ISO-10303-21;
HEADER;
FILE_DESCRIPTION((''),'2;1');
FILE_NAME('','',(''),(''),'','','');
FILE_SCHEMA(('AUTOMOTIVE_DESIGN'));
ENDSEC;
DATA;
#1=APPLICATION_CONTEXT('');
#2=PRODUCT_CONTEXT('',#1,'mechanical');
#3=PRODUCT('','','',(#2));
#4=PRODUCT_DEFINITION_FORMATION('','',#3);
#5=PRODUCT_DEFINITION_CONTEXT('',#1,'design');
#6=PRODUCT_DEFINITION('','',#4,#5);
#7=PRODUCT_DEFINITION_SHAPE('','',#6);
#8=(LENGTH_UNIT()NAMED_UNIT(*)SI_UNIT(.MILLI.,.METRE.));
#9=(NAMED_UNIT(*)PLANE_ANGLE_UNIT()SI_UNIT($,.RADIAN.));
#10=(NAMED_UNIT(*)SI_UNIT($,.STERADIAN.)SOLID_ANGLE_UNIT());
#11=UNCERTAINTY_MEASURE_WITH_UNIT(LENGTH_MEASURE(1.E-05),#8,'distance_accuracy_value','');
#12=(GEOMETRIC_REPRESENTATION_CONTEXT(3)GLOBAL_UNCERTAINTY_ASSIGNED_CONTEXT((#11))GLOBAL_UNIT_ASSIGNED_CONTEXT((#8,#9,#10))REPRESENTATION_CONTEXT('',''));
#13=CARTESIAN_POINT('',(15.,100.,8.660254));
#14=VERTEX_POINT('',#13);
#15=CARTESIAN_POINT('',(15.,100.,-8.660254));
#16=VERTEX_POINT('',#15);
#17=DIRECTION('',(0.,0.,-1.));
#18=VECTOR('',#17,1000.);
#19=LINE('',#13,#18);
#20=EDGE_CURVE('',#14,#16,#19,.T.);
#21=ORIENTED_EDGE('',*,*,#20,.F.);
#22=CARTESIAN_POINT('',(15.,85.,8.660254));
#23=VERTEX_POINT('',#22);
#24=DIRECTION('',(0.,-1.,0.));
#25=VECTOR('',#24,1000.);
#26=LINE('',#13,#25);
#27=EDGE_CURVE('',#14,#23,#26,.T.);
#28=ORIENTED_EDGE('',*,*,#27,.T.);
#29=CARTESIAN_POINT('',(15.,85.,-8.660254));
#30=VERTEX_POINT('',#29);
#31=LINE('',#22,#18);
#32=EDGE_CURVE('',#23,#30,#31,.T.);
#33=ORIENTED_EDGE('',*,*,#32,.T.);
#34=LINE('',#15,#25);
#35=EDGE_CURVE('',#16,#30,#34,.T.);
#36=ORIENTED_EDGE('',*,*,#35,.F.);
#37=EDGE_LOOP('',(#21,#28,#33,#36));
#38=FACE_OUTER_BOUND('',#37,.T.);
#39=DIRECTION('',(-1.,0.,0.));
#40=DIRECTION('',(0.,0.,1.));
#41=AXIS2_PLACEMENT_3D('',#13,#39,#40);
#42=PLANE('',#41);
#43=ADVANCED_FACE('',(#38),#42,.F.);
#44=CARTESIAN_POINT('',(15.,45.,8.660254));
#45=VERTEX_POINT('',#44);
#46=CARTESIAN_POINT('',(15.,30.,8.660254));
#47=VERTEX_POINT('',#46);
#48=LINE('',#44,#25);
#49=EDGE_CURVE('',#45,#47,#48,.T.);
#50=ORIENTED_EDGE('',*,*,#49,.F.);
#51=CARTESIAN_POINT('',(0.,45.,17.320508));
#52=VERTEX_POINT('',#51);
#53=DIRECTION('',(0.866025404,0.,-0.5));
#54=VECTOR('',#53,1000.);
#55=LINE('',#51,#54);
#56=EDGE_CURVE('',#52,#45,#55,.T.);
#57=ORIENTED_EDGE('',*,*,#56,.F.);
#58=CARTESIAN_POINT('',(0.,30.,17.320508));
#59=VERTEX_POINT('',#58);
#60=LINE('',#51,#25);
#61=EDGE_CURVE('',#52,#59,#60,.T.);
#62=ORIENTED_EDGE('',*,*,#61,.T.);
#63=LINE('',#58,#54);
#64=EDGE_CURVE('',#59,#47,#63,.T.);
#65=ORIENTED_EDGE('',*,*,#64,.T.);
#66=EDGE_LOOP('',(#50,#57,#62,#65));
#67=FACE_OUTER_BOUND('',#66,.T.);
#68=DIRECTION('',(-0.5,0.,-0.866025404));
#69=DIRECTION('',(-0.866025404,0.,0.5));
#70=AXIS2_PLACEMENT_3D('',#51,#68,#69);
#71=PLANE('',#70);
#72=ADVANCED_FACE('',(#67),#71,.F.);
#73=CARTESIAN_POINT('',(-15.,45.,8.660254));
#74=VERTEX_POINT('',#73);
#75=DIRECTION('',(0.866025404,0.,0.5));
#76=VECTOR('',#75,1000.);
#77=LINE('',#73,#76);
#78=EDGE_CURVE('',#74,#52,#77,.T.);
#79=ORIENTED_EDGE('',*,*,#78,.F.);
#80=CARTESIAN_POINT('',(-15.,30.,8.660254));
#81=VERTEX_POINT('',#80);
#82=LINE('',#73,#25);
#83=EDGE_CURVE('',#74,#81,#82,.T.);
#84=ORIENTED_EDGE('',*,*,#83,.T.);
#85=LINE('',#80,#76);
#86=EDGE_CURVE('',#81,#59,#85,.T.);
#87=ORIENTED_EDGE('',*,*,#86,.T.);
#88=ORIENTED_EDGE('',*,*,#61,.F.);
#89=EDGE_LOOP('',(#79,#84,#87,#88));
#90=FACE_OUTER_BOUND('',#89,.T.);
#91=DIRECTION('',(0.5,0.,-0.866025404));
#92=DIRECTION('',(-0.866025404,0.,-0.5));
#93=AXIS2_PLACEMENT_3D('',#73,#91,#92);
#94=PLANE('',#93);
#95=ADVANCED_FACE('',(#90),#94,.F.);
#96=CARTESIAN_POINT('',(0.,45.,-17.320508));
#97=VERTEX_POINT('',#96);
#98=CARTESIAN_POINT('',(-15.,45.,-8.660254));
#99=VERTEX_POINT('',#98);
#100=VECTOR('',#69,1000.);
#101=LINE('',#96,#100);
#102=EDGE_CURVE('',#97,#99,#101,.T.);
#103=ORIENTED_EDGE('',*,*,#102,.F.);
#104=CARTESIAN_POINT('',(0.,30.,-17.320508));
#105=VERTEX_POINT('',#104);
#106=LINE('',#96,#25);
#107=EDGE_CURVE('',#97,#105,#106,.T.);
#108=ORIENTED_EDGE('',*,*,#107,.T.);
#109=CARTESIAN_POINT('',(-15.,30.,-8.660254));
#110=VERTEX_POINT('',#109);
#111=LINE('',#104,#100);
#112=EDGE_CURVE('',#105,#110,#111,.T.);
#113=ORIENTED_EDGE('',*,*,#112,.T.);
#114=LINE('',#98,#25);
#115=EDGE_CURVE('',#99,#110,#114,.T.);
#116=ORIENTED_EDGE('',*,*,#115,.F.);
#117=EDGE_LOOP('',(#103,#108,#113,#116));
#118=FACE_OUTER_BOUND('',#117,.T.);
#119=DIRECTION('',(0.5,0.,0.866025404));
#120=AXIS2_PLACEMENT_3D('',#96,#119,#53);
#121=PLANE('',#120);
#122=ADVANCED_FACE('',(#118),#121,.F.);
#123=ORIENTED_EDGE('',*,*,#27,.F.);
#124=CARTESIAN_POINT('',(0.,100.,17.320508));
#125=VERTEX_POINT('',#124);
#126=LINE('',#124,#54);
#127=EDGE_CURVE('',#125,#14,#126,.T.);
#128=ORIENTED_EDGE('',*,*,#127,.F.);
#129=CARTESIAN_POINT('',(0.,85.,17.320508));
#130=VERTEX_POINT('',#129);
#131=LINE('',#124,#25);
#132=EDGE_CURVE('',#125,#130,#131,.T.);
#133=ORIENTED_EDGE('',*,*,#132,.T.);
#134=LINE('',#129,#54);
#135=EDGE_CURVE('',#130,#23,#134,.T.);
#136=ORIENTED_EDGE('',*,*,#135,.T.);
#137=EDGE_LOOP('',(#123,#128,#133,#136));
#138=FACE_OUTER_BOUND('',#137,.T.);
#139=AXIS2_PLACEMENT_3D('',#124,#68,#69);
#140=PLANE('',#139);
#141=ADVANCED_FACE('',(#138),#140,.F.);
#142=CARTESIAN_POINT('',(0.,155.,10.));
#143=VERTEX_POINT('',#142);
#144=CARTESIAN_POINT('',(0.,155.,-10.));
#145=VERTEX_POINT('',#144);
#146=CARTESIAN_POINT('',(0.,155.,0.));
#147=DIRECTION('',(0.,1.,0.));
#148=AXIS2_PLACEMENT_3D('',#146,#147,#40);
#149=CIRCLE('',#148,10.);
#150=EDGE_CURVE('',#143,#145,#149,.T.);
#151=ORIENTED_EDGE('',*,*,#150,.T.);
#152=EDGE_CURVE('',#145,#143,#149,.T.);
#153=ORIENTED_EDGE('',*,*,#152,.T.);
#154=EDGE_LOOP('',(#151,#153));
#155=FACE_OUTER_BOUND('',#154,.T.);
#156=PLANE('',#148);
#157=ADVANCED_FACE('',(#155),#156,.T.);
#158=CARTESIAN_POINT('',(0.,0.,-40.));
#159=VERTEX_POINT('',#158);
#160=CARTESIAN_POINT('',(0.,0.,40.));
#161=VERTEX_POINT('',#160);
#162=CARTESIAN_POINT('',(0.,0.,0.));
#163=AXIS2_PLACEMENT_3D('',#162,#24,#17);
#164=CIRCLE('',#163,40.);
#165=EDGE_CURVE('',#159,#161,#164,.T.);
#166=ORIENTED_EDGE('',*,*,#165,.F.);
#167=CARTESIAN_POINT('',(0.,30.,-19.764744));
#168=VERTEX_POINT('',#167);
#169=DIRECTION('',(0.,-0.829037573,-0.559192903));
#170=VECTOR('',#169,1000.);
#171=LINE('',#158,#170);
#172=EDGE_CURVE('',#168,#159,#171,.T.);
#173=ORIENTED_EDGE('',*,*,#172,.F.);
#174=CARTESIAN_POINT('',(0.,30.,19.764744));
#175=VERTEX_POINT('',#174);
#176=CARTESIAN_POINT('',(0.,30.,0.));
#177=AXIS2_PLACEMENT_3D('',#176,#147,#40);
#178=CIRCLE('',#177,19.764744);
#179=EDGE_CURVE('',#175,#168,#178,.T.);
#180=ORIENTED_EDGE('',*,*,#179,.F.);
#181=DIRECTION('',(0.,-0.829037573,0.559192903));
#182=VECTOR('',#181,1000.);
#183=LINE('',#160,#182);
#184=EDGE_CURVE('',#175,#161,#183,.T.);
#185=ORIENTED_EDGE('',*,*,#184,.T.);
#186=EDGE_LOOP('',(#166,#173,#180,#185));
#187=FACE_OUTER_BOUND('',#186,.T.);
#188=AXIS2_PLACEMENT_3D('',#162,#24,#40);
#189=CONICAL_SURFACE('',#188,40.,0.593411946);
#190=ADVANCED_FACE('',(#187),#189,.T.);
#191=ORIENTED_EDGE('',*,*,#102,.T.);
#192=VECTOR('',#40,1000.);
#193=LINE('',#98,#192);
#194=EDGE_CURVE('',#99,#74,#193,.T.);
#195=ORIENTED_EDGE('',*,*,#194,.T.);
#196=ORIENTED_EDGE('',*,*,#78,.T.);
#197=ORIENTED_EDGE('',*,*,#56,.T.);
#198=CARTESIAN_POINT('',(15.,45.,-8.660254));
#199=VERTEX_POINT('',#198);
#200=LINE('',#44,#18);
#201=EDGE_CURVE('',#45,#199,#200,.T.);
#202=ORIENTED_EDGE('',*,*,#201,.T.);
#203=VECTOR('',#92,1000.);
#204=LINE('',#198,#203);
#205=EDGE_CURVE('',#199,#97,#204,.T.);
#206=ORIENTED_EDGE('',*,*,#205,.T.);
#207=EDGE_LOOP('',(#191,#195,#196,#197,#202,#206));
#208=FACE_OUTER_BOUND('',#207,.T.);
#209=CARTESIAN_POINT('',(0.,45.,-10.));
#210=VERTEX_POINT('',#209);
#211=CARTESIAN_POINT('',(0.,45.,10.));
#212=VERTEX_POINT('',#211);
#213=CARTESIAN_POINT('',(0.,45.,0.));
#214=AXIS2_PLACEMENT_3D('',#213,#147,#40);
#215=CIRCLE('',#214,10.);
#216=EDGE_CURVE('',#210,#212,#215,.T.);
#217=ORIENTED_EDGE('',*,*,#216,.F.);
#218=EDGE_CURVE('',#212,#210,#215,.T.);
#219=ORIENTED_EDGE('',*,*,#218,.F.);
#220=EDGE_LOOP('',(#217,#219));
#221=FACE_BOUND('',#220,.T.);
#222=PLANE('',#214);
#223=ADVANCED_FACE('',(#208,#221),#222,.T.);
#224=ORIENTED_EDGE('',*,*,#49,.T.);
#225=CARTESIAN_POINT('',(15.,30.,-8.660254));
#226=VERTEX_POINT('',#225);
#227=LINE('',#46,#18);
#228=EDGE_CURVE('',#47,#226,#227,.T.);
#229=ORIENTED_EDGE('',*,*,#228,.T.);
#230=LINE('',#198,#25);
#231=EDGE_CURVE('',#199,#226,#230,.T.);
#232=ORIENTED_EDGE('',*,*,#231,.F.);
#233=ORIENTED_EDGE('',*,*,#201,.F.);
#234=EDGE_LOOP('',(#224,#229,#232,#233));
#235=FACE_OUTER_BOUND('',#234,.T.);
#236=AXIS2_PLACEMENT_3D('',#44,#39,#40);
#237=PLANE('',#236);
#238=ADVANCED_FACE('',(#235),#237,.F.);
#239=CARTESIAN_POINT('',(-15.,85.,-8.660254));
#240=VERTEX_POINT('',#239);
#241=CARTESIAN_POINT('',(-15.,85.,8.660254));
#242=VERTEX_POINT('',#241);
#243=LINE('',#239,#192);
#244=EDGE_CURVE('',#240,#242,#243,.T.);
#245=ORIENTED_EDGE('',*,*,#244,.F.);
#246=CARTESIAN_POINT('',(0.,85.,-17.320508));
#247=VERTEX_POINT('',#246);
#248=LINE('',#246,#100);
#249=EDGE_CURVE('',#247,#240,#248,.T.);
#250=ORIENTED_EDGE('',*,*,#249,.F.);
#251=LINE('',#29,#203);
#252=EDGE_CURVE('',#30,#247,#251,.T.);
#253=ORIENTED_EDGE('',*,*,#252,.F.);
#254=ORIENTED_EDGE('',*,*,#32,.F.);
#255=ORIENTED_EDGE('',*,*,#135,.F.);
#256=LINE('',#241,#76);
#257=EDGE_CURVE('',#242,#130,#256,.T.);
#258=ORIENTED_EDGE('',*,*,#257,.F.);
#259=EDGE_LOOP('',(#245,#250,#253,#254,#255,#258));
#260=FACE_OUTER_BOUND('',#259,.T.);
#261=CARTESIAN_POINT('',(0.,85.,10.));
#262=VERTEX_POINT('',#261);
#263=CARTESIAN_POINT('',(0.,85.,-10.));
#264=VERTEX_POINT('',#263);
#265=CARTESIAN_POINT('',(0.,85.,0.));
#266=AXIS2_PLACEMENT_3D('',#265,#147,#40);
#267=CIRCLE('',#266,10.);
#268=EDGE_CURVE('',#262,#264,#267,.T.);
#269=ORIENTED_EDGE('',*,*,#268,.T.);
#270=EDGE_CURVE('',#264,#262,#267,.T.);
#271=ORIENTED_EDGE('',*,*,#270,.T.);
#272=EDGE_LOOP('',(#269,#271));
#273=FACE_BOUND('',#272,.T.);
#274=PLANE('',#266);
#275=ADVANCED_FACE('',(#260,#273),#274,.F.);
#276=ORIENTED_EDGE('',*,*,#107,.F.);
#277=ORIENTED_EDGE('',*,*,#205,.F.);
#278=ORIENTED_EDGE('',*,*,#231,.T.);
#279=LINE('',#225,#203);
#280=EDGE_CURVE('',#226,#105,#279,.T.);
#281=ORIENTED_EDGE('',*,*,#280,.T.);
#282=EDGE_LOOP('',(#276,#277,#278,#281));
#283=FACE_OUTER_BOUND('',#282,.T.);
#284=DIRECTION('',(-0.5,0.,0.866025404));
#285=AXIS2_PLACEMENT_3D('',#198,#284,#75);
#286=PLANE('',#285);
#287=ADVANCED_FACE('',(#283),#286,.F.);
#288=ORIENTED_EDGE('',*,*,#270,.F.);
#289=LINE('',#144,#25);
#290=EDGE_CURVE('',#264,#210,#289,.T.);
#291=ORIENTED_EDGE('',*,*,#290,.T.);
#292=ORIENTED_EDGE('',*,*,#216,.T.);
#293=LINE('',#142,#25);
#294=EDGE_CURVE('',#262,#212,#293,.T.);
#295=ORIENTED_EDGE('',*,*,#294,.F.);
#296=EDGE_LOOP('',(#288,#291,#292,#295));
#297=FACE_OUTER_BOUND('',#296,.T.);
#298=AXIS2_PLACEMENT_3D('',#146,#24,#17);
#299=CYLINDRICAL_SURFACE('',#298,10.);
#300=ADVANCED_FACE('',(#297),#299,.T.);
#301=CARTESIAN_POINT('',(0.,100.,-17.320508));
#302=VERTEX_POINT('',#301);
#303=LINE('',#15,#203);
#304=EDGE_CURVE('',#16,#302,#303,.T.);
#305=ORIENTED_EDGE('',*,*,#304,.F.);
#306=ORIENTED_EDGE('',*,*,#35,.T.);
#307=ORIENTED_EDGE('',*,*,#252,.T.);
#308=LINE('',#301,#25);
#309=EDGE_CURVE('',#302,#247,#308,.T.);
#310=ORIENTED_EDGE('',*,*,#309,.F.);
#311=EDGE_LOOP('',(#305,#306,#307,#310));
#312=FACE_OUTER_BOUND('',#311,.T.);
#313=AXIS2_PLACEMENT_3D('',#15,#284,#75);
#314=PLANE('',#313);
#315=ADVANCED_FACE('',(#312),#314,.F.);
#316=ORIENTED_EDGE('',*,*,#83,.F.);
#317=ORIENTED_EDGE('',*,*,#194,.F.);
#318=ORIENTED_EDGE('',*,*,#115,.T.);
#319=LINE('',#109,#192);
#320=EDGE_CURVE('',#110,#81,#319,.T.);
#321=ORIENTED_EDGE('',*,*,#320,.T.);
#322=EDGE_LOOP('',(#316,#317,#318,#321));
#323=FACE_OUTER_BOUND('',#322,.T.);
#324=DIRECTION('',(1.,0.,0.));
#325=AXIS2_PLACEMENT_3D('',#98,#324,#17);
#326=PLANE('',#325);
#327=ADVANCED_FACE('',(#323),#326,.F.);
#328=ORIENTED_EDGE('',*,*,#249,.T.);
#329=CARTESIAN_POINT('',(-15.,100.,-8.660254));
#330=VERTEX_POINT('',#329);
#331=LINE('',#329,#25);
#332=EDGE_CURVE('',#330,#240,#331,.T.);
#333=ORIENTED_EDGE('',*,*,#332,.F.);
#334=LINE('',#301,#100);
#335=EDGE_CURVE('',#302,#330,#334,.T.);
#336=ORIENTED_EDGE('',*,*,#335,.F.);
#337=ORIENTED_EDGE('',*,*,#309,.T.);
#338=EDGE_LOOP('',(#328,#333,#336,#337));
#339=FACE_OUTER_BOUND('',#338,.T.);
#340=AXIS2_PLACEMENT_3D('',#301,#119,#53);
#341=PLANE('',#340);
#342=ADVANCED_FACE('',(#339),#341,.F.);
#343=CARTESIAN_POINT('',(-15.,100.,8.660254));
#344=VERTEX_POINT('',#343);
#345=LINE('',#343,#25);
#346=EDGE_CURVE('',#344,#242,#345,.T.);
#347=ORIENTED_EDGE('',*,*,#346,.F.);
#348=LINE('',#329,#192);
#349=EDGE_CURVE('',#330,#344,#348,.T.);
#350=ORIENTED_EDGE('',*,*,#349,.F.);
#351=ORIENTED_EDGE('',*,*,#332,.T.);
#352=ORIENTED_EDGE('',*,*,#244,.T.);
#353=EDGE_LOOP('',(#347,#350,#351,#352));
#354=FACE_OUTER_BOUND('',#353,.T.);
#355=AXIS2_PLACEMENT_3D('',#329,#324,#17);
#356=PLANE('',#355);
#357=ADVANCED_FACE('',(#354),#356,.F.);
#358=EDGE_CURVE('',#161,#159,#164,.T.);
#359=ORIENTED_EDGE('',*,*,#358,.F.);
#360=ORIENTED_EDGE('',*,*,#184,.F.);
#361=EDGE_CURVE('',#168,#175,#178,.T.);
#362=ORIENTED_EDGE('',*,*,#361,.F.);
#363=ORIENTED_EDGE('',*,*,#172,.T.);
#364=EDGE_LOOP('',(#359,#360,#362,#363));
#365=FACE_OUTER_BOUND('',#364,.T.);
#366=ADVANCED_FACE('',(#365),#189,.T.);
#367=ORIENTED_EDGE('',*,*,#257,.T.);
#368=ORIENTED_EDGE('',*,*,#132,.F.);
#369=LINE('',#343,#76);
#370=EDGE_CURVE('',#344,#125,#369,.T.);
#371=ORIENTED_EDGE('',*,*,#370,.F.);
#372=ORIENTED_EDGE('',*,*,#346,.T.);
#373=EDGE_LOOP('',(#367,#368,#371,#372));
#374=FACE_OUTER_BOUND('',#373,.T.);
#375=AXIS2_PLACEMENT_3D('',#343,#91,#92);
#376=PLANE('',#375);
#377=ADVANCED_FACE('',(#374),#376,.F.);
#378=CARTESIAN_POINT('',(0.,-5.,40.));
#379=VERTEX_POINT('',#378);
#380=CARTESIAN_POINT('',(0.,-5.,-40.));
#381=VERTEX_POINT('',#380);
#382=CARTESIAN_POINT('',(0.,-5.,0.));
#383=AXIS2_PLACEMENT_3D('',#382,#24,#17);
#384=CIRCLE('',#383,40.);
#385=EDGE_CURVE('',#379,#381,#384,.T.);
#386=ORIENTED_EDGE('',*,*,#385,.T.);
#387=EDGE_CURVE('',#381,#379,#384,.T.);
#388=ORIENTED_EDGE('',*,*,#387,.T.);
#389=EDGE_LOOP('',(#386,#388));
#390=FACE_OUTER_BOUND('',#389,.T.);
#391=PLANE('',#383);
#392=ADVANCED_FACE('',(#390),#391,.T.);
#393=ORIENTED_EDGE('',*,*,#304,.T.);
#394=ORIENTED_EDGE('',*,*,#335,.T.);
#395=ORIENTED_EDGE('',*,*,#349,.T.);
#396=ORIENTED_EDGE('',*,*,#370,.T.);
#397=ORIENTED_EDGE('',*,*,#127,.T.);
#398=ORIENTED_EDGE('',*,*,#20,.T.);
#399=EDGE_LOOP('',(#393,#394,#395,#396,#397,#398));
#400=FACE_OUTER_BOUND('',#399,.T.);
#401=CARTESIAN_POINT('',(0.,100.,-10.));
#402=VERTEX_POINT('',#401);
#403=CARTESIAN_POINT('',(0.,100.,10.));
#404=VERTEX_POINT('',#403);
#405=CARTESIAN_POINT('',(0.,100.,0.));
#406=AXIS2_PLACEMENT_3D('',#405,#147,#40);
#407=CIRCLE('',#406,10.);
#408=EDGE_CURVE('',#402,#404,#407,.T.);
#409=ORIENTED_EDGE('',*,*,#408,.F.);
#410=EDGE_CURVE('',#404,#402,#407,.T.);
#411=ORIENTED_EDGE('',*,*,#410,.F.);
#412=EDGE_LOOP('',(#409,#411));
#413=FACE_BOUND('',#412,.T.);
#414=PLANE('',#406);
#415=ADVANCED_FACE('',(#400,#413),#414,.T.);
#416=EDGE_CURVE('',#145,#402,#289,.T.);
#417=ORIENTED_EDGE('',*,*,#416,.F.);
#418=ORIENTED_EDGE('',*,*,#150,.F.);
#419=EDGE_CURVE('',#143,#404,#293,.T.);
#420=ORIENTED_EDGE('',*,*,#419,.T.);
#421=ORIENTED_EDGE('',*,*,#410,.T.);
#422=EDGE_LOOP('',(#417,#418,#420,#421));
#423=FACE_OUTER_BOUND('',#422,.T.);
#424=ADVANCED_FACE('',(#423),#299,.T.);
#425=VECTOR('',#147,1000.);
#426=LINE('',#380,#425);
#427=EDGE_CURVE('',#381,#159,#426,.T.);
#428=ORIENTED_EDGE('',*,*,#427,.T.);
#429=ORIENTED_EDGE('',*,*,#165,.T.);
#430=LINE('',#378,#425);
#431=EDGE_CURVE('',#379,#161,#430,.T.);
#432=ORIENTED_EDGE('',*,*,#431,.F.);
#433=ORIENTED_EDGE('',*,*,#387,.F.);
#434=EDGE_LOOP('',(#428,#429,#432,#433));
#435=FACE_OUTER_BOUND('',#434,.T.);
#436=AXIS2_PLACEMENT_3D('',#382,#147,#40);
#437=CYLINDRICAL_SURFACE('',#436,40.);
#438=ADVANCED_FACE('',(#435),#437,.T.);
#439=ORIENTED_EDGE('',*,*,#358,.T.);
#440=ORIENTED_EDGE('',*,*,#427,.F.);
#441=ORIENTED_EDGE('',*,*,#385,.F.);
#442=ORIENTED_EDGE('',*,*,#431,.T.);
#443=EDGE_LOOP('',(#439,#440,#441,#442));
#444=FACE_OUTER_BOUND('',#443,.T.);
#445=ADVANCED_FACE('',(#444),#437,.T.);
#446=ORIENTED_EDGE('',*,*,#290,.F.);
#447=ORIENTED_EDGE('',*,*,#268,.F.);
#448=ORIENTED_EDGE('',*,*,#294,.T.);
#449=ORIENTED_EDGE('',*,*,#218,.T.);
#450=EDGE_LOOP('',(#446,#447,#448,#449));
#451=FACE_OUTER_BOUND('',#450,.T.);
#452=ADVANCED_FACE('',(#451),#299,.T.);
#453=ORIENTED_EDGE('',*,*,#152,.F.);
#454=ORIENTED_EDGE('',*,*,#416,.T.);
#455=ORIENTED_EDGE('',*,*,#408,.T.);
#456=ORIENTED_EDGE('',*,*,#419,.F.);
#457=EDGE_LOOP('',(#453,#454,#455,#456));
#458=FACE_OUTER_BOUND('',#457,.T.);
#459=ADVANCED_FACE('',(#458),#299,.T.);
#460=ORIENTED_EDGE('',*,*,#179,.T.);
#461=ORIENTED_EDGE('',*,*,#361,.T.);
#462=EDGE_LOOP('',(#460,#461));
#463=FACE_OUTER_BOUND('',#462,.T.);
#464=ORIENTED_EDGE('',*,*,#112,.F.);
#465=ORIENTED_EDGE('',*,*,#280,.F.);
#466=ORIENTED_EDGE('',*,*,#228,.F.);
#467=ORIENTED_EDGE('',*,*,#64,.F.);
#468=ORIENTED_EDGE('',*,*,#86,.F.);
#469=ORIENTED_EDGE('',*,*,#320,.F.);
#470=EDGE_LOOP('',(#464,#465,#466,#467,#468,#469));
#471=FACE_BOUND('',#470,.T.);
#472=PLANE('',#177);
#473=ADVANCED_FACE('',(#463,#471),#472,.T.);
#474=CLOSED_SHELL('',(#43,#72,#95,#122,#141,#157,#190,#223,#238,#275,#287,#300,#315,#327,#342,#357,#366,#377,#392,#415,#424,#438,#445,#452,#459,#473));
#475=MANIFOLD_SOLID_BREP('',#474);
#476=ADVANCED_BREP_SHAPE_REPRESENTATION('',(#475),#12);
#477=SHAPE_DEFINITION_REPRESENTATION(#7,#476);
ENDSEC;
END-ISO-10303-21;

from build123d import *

# Parameters (mm, degrees)
SKETCH_1_R      = 40
EXTRUDE_1_DEPTH = 30
EXTRUDE_1_TAPER = 34
SKETCH_2_R      = 10
EXTRUDE_2_DEPTH = 125
EXTRUDE_3_DEPTH = 15
SKETCH_4_R      = 40
EXTRUDE_4_DEPTH = 5
EXTRUDE_START   = 40
EXTRUDE_5_DEPTH = 15


with BuildPart() as part:
    # 草图1 → 凸台-拉伸1 (new body)
    with BuildSketch(Plane(origin=(0, 0, 0), x_dir=(1, 0, 0), z_dir=(0, 1, 0))):
        Circle(SKETCH_1_R)
    extrude(amount=EXTRUDE_1_DEPTH, taper=EXTRUDE_1_TAPER)

    # 草图2 → 凸台-拉伸2 (add)
    with BuildSketch(Plane(origin=(0, 30, 0), x_dir=(1, 0, 0), z_dir=(0, 1, 0))):
        with Locations(Location((0, 0, 0), (0, 0, 270))):
            Circle(SKETCH_2_R)
    extrude(amount=EXTRUDE_2_DEPTH)

    # 草图3 → 凸台-拉伸3 (add)
    with BuildSketch(Plane(origin=(0, 30, 0), x_dir=(1, 0, 0), z_dir=(0, 1, 0))):
        Polygon((15, -8.660254038), (15, 8.660254038), (0, 17.320508076), (-15, 8.660254038), (-15, -8.660254038), (0, -17.320508076), align=None)
    extrude(amount=EXTRUDE_3_DEPTH)

    # 草图4 → 凸台-拉伸4 (add)
    with BuildSketch(Plane.XZ):
        with Locations(Location((0, 0, 0), (0, 0, 270))):
            Circle(SKETCH_4_R)
    extrude(amount=EXTRUDE_4_DEPTH)

    # 草图5 → 凸台-拉伸5 (add)
    with BuildSketch(Plane(origin=(0, 45, 0), x_dir=(1, 0, 0), z_dir=(0, 1, 0)).offset(EXTRUDE_START)):
        Polygon((0, -17.320508076), (15, -8.660254038), (15, 8.660254038), (0, 17.320508076), (-15, 8.660254038), (-15, -8.660254038), align=None)
    extrude(amount=EXTRUDE_5_DEPTH)


solid = part.part
